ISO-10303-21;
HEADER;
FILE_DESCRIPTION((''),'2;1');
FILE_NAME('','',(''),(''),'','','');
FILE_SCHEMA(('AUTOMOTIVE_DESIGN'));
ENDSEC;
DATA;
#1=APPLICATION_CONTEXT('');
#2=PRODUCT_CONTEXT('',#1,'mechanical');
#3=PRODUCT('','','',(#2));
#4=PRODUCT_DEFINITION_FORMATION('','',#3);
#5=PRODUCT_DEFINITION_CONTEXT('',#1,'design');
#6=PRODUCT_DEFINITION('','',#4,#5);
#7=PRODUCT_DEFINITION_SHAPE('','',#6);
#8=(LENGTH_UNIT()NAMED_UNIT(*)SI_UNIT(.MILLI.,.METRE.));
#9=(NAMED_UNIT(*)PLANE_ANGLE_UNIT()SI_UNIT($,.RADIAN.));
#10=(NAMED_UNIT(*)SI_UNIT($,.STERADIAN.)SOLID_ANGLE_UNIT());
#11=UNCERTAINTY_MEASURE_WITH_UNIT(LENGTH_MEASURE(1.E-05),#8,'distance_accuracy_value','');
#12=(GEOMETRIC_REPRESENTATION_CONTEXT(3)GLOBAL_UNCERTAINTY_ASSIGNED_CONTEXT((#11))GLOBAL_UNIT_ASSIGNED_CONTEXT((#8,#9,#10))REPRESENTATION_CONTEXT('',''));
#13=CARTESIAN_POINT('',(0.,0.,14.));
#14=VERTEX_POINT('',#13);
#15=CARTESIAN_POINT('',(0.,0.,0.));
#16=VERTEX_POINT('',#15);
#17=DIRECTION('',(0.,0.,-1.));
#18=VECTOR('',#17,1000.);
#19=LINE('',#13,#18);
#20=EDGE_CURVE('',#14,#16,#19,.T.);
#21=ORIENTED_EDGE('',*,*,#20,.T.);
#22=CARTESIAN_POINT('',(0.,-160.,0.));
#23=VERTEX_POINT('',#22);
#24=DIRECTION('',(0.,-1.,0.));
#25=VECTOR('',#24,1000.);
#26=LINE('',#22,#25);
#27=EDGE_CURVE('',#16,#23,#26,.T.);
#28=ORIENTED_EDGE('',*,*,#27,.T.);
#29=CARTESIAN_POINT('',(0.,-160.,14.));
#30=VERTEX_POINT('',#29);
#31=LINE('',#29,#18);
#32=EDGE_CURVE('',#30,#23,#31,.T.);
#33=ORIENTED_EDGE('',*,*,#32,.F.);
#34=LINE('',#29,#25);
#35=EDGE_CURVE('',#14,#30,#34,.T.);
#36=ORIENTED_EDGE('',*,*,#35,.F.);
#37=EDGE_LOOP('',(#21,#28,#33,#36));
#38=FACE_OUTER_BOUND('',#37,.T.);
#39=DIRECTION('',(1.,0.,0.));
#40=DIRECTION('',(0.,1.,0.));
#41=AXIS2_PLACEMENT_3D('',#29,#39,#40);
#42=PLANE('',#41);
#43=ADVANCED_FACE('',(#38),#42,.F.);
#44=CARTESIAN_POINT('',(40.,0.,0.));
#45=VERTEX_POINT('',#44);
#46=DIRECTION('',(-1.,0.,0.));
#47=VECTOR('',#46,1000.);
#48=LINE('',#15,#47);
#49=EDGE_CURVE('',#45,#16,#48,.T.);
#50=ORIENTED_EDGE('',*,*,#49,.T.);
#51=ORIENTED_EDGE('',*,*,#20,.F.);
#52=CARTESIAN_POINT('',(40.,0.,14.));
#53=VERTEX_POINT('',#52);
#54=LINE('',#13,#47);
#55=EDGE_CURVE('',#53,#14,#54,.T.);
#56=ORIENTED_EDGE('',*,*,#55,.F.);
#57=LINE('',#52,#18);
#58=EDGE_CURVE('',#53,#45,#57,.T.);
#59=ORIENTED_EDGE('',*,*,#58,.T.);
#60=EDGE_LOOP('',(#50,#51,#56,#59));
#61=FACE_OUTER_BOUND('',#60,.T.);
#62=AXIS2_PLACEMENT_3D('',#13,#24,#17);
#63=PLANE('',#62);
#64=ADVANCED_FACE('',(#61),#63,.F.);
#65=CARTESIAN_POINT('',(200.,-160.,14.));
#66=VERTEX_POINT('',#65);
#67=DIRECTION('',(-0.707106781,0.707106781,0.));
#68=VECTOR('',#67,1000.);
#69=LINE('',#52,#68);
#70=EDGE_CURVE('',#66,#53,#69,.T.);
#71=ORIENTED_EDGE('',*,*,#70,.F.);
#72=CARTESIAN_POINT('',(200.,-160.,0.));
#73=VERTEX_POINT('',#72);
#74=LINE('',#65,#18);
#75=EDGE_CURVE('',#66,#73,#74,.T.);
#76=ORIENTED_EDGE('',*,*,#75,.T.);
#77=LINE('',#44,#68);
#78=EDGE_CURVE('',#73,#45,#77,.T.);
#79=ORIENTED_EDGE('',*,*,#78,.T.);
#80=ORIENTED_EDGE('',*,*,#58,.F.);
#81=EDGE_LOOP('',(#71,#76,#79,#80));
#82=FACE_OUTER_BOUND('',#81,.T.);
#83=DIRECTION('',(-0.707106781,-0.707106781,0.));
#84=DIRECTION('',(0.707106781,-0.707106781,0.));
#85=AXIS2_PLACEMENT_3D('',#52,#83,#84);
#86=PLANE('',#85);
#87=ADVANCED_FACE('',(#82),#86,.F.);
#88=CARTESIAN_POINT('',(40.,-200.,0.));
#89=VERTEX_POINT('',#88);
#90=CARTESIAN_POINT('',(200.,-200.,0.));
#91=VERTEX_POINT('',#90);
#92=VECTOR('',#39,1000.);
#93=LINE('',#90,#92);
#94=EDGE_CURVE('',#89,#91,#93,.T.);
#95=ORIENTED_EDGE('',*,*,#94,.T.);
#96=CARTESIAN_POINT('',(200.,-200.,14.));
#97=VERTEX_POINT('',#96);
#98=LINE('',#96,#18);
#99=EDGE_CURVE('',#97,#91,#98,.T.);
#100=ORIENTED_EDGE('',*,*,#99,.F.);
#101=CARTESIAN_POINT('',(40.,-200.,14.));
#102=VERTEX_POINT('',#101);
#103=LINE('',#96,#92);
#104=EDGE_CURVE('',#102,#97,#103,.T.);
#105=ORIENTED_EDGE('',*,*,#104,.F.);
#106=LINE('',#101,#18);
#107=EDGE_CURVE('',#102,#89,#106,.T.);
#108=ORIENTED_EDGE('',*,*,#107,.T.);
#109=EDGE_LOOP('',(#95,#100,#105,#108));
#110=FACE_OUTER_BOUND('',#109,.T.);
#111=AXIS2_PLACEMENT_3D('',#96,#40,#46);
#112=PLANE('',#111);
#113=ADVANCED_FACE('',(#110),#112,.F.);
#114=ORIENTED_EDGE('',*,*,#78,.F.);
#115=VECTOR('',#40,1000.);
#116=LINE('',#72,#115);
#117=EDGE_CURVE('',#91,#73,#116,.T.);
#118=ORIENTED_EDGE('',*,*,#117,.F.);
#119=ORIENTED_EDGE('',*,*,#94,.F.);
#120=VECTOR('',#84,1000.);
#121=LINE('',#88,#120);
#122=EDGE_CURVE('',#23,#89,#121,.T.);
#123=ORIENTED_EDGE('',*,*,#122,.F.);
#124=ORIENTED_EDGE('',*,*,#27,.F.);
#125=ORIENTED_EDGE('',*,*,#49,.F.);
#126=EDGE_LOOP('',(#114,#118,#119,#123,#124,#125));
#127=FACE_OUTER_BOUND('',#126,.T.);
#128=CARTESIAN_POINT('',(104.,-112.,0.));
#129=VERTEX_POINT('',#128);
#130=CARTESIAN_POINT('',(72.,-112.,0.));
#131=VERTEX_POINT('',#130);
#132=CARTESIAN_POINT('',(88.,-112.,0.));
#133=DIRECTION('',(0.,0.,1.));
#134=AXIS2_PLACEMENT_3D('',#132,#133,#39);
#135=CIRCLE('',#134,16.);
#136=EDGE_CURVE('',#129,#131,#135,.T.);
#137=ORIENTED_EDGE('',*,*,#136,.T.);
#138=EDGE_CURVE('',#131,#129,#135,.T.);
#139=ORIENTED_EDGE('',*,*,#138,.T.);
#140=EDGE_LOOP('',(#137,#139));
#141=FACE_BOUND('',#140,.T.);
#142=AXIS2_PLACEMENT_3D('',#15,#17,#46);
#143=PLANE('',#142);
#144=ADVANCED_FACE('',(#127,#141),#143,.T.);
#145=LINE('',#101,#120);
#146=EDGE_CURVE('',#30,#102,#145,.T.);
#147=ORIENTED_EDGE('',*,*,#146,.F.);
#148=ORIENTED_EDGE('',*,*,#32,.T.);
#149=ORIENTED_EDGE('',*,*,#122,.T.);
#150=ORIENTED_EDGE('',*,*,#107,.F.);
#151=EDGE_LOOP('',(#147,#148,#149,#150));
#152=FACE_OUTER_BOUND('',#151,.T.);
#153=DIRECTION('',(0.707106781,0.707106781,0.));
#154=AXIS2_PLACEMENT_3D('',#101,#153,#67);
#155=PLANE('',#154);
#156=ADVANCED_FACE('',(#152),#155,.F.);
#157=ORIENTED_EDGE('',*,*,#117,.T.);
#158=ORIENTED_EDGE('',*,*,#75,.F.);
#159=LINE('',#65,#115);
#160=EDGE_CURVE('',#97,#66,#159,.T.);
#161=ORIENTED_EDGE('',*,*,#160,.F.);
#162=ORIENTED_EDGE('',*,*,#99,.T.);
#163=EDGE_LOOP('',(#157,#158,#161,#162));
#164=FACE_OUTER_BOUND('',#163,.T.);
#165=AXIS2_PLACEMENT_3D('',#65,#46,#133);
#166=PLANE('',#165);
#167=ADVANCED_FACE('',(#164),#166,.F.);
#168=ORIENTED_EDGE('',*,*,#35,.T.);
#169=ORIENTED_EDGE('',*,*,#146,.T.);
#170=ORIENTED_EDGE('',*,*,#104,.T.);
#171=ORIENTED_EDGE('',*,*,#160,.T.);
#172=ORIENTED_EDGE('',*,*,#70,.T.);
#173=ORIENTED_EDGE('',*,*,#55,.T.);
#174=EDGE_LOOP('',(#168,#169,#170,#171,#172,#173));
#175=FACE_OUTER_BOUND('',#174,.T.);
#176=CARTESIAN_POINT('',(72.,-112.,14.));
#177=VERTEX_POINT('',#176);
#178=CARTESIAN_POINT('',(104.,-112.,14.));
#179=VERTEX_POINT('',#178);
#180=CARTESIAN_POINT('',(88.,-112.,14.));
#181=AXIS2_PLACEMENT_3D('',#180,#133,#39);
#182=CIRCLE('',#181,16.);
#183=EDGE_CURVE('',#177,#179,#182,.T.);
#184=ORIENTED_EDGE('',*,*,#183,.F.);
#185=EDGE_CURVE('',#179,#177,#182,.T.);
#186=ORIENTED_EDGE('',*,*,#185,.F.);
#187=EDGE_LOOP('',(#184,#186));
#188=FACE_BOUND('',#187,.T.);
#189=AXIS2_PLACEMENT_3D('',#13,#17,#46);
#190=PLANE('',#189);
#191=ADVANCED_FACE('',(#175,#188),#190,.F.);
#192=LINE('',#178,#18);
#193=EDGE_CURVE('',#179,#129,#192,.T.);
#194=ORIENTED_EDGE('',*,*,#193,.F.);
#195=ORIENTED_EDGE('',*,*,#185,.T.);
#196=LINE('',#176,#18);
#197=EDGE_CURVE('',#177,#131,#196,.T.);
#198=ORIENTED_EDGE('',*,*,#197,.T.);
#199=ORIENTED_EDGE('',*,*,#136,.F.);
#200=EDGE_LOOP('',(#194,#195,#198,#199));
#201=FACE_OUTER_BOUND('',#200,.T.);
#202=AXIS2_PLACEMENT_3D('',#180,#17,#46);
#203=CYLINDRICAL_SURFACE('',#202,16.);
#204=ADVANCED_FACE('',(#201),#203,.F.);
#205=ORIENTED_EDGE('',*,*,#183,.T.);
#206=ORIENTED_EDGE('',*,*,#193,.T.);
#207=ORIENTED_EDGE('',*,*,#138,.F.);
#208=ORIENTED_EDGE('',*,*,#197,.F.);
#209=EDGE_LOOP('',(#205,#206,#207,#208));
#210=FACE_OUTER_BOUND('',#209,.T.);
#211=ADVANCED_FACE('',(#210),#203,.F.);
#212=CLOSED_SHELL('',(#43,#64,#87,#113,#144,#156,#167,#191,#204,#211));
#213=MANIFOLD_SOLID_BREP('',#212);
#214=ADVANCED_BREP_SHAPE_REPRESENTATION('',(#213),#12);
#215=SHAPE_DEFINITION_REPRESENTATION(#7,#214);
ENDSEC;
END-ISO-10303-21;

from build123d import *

# Parameters (mm, degrees)
SKETCH1_R           = 16
BOSS_EXTRUDE1_DEPTH = 14


with BuildPart() as part:
    # Sketch1 → Boss-Extrude1 (new body)
    with BuildSketch(Plane.XY):
        Polygon((0, 0), (40, 0), (200, -160), (200, -200), (40, -200), (0, -160), align=None)
        with Locations((88, -112)):
            Circle(SKETCH1_R, mode=Mode.SUBTRACT)
    extrude(amount=BOSS_EXTRUDE1_DEPTH)


solid = part.part
